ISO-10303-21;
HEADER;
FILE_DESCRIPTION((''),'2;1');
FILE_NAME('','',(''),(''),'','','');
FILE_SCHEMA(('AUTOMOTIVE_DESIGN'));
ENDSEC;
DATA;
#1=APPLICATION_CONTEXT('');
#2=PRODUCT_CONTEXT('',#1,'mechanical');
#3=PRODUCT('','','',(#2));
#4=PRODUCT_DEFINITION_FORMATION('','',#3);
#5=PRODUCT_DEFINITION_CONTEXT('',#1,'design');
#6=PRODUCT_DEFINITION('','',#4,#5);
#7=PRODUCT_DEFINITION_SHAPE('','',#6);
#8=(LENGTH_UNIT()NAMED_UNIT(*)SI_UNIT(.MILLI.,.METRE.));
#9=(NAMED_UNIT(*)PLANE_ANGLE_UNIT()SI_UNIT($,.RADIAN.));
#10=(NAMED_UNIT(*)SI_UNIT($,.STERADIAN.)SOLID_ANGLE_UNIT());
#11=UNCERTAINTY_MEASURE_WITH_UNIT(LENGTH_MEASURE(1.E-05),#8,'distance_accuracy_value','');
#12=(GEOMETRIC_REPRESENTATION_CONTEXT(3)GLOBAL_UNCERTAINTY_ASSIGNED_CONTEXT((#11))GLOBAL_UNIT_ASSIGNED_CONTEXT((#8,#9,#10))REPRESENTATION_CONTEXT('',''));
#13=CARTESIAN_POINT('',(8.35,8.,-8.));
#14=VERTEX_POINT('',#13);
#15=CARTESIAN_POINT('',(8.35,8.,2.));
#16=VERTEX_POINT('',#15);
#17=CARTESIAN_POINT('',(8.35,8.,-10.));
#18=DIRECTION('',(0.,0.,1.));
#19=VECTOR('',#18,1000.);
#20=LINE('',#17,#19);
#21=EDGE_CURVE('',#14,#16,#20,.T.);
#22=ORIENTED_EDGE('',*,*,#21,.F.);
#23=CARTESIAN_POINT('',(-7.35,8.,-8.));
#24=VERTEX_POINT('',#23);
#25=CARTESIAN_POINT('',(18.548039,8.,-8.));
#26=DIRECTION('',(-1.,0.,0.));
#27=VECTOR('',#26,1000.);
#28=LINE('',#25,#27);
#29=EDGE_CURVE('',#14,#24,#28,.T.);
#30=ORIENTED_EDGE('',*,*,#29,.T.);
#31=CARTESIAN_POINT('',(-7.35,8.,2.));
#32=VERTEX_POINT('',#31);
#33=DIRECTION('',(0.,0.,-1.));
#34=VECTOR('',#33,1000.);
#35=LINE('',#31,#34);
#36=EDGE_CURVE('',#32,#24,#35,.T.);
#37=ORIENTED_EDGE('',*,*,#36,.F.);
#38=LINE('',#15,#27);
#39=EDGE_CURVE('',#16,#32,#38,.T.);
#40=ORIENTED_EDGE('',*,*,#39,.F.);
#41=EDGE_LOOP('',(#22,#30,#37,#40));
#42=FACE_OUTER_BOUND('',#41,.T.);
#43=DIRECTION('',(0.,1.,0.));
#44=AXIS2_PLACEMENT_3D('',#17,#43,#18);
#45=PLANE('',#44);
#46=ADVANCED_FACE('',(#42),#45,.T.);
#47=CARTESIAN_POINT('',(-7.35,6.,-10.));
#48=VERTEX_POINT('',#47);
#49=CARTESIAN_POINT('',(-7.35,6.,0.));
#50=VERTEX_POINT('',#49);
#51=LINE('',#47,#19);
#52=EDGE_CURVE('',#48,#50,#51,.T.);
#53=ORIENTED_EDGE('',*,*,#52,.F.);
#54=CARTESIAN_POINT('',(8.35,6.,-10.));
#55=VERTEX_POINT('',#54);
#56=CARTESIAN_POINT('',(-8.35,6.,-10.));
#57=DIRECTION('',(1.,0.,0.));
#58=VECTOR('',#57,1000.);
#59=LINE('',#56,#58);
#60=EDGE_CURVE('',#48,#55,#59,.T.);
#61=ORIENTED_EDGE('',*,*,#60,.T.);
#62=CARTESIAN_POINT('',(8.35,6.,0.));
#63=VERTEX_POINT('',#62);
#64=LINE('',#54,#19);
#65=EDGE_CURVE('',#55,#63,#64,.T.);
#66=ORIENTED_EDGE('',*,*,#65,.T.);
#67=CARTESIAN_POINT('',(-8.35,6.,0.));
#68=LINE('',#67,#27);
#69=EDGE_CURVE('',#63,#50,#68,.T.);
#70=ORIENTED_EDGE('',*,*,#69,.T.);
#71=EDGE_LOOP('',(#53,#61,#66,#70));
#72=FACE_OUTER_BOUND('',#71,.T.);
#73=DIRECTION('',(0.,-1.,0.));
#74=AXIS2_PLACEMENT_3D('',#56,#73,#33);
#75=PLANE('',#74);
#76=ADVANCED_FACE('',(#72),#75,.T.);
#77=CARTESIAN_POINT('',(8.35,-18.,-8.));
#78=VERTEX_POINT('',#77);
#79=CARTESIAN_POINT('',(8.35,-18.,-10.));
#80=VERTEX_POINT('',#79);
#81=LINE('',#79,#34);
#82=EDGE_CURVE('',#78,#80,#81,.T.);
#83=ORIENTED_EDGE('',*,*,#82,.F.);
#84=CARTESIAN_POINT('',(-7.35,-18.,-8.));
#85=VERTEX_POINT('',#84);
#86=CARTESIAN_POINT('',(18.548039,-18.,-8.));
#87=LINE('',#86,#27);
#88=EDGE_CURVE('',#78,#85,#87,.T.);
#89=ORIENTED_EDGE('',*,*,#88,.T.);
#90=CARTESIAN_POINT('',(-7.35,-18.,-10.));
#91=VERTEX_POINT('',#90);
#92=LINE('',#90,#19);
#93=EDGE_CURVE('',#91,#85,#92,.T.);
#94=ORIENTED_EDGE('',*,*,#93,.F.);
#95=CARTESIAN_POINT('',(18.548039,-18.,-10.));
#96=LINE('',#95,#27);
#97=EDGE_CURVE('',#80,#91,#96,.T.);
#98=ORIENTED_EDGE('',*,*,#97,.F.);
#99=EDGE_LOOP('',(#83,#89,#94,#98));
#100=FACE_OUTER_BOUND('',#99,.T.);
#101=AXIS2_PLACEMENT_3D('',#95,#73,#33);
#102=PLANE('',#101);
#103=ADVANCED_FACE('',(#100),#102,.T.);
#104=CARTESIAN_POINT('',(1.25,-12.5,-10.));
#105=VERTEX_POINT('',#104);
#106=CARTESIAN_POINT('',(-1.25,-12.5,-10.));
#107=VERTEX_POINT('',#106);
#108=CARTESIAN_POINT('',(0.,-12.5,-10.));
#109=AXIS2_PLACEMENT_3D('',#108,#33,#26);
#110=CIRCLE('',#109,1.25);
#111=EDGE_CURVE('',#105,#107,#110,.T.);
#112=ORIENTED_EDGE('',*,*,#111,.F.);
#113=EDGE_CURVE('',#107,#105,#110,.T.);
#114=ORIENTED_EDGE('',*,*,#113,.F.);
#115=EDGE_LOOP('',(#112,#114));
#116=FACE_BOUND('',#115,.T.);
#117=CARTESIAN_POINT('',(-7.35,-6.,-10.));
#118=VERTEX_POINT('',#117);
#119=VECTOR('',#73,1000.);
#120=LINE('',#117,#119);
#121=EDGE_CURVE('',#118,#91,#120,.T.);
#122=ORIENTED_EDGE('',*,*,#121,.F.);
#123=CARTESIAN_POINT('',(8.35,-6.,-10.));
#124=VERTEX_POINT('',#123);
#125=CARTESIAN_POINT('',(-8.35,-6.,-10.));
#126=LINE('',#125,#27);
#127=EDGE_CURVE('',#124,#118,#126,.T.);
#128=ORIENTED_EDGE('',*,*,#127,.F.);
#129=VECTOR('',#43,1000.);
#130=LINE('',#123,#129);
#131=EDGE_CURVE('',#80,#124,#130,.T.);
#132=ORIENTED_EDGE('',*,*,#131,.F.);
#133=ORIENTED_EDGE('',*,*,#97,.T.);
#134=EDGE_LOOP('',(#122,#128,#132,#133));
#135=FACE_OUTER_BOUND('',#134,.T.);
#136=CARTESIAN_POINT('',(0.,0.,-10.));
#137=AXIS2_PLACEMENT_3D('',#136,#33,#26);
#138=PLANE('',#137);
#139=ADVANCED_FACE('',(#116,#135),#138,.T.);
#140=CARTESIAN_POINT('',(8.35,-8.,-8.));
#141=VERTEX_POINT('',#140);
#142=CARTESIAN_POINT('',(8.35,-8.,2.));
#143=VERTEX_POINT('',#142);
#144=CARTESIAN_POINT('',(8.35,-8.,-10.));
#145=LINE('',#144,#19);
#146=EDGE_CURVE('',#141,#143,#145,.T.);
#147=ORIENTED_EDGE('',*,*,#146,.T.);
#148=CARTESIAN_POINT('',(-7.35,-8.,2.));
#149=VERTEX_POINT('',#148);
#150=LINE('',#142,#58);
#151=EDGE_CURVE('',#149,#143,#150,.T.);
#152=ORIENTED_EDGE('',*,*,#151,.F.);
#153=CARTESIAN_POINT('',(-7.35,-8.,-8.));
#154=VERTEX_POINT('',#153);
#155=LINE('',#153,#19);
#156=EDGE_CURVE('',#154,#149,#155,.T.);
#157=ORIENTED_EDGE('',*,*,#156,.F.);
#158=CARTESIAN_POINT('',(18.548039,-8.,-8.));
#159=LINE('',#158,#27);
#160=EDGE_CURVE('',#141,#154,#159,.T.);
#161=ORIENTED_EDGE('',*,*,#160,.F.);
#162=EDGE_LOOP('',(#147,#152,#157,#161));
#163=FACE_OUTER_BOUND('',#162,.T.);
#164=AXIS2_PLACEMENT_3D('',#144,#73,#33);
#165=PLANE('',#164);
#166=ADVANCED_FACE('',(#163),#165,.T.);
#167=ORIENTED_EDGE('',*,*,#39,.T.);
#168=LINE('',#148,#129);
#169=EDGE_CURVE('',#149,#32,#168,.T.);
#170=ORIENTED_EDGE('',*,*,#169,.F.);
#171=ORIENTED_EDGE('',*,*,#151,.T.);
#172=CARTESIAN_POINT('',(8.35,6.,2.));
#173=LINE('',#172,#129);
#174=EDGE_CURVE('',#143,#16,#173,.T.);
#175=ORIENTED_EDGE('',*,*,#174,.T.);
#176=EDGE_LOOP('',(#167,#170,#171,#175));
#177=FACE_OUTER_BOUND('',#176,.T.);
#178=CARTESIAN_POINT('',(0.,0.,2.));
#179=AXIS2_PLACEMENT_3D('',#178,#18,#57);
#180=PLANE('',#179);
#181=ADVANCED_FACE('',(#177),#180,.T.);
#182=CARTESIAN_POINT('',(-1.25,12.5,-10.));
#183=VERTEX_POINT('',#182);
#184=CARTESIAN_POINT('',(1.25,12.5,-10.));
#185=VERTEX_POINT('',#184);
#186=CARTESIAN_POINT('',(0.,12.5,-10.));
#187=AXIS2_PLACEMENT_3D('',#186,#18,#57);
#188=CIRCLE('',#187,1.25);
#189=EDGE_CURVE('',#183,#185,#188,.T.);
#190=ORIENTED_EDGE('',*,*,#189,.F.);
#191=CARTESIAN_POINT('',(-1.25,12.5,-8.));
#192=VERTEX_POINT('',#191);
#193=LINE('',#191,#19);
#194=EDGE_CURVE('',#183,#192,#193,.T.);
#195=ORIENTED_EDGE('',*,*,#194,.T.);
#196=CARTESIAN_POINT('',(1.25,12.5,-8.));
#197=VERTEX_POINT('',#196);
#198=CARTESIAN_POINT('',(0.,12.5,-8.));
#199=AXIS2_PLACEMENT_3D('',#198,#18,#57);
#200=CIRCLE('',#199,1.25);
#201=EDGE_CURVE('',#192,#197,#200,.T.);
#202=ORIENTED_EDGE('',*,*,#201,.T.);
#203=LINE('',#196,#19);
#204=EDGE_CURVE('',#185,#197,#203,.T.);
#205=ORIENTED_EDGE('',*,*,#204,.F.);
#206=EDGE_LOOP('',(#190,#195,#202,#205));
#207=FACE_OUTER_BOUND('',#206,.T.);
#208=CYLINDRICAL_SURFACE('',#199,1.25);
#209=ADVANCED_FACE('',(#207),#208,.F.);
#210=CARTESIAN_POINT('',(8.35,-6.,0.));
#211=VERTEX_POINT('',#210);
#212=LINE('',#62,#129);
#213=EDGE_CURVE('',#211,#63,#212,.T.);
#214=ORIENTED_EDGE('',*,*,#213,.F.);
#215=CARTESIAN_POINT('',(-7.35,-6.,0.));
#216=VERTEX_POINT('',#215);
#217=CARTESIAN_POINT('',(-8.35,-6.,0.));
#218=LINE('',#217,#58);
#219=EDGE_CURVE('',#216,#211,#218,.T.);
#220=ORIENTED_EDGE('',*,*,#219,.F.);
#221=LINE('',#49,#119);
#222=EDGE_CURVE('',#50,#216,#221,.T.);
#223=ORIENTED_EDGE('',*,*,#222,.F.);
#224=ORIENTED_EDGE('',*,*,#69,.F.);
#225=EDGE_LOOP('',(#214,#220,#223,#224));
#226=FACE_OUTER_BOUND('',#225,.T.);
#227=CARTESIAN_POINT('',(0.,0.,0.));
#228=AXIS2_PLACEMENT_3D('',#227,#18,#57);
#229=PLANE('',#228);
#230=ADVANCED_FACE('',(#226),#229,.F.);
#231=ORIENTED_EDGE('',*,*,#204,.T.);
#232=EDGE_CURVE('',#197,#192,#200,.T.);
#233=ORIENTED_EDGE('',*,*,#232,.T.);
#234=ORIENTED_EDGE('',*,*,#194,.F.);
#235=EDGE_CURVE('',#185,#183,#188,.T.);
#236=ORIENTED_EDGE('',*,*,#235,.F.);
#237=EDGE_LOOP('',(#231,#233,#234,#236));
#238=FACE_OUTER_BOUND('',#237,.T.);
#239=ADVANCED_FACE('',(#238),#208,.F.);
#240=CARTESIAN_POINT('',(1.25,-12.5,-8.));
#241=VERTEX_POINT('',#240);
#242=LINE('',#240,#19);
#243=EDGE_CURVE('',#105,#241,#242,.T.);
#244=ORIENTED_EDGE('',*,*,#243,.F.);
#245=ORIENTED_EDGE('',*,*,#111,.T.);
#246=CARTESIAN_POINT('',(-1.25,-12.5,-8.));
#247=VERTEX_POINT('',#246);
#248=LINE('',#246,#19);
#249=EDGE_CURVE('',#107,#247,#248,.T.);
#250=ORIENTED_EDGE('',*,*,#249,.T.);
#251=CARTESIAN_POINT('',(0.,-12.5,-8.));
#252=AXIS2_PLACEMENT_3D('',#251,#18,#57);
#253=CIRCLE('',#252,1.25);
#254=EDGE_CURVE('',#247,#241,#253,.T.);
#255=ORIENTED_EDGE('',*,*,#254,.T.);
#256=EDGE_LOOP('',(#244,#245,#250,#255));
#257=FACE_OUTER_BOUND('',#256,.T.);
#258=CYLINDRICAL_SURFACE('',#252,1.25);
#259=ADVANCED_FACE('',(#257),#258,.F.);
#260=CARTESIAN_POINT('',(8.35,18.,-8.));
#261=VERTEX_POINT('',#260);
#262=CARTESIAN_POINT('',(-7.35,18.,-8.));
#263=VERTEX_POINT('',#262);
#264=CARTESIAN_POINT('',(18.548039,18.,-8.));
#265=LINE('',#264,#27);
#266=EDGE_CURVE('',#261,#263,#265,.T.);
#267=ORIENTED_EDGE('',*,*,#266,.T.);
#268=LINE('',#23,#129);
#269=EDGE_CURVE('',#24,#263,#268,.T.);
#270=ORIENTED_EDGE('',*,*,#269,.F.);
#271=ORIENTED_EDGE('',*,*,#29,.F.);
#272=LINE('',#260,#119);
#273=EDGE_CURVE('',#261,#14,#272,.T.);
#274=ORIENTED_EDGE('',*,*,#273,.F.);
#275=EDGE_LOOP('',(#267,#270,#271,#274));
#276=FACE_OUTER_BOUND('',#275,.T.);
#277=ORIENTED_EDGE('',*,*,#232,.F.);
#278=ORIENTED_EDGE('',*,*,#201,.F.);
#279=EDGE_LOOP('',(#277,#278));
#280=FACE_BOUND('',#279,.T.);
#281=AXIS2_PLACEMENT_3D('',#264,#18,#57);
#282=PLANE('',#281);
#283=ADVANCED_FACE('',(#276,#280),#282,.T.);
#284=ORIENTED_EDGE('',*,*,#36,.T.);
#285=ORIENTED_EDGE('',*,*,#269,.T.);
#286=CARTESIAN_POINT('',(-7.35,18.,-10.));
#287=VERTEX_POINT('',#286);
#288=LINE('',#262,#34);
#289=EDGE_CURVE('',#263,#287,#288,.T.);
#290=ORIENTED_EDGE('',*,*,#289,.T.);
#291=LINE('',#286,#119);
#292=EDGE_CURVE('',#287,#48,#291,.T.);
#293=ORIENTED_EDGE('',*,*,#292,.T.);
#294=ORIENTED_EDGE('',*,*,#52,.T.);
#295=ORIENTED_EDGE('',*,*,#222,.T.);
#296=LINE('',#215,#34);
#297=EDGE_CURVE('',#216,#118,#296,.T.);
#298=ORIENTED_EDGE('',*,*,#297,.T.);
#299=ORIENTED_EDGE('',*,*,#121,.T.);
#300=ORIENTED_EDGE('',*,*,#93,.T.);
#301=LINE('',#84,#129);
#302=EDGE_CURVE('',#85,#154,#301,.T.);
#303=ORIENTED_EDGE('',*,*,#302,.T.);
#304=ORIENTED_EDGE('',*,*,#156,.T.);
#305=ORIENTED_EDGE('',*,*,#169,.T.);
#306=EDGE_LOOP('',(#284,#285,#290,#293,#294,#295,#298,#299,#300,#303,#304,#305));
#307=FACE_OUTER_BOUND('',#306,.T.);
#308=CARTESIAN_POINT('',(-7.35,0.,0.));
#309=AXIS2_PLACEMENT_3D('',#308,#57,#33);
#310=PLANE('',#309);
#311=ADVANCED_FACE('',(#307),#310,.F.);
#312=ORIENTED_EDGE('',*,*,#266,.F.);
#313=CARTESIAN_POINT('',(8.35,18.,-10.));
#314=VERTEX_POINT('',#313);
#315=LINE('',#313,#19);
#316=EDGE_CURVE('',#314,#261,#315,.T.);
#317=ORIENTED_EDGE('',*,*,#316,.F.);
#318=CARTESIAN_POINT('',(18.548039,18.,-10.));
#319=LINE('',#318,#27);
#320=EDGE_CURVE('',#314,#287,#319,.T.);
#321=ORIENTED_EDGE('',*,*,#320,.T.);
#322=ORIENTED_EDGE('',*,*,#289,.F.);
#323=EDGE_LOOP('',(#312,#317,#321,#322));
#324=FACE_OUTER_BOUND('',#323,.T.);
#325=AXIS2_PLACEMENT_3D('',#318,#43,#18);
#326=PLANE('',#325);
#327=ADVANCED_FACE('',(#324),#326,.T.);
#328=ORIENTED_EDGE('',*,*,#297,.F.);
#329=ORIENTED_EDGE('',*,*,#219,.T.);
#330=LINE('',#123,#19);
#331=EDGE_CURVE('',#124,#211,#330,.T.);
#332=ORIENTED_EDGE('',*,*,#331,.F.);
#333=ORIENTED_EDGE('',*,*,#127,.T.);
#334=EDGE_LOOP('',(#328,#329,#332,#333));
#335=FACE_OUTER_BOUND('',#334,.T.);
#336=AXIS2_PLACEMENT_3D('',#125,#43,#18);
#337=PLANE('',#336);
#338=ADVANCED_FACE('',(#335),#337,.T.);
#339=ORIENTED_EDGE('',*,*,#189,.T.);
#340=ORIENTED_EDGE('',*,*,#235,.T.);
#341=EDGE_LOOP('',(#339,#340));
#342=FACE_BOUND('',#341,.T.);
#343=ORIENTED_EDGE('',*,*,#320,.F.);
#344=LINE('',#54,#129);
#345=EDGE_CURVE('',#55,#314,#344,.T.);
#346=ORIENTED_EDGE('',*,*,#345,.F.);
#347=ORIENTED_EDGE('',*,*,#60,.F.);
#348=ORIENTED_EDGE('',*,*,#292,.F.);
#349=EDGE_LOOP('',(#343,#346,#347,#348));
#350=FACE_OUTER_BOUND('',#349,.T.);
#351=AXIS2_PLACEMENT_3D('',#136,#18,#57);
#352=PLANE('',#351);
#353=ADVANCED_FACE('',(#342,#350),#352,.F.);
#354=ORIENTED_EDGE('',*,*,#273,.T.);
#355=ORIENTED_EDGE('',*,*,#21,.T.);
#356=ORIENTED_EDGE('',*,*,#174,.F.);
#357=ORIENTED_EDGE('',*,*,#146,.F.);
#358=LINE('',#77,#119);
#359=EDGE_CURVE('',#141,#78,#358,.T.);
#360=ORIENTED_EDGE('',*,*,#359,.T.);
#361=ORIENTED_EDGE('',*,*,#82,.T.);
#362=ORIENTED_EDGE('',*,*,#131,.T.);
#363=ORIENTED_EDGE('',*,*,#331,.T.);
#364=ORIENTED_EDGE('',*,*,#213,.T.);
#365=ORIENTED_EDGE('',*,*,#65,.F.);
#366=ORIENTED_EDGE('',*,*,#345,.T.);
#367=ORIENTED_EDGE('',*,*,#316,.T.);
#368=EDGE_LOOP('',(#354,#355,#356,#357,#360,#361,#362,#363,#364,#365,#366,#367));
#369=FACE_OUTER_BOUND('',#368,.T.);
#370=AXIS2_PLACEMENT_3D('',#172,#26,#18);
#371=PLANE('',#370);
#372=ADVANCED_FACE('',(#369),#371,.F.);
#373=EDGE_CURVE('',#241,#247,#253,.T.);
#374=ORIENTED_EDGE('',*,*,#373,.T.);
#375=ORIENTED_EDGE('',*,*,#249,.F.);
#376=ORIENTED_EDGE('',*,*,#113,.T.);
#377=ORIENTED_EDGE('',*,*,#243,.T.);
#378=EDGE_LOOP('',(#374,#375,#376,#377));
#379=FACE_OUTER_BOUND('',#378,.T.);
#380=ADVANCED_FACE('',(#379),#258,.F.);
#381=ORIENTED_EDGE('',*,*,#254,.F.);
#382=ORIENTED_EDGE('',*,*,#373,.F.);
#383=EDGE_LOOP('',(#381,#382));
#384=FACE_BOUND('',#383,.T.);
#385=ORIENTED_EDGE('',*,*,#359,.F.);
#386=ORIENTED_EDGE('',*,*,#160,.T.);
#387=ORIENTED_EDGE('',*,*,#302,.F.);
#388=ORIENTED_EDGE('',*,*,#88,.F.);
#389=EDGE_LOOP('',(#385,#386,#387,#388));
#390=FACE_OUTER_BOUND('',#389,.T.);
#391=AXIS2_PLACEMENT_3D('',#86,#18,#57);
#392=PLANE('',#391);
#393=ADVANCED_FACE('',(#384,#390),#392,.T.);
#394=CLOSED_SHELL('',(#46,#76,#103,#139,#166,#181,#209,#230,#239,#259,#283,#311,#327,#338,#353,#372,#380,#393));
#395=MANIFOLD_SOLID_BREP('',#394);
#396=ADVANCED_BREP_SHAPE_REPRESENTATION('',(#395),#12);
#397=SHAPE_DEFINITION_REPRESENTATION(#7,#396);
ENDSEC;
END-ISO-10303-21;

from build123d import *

# Parameters (mm, degrees)
SKETCH1_W           = 16.7
SKETCH1_H           = 12
BOSS_EXTRUDE1_DEPTH = 2
SKETCH2_W           = 16.7
SKETCH2_H           = 2
BOSS_EXTRUDE2_DEPTH = 12
SKETCH4_W           = 2
SKETCH4_H           = 10
BOSS_EXTRUDE3_DEPTH = 16.7
M3_TAPPED_HOLE1_D   = 2.5
CUT_EXTRUDE1_DEPTH  = 1


with BuildPart() as part:
    # Sketch1 → Boss-Extrude1 (new body)
    with BuildSketch(Plane.XY):
        Rectangle(SKETCH1_W, SKETCH1_H)
    extrude(amount=BOSS_EXTRUDE1_DEPTH)

    # Sketch2 → Boss-Extrude2 (add)
    with BuildSketch(Plane.XY.offset(2)):
        with Locations((0, 7)):
            Rectangle(SKETCH2_W, SKETCH2_H)
        with Locations((0, -7)):
            Rectangle(SKETCH2_W, SKETCH2_H)
    extrude(amount=-BOSS_EXTRUDE2_DEPTH)

    # Sketch4 → Boss-Extrude3 (add)
    with BuildSketch(Plane.ZY.offset(8.35)):
        with Locations((-9, -13)):
            Rectangle(SKETCH4_W, SKETCH4_H)
        with Locations((-9, 13)):
            Rectangle(SKETCH4_W, SKETCH4_H)
    extrude(amount=-BOSS_EXTRUDE3_DEPTH)

    # M3 Tapped Hole1 (through all)
    with Locations(Plane.XY.offset(-8)):
        with Locations((0, -12.5), (0, 12.5)):
            Hole(M3_TAPPED_HOLE1_D / 2)

    # Sketch8 → Cut-Extrude1 (cut)
    with BuildSketch(Plane.ZY.offset(8.35)):
        Polygon((0, 6), (0, -6), (-10, -6), (-10, -18), (-8, -18), (-8, -8), (2, -8), (2, 8), (-8, 8), (-8, 18), (-10, 18), (-10, 6), align=None)
    extrude(amount=-CUT_EXTRUDE1_DEPTH, mode=Mode.SUBTRACT)


solid = part.part
